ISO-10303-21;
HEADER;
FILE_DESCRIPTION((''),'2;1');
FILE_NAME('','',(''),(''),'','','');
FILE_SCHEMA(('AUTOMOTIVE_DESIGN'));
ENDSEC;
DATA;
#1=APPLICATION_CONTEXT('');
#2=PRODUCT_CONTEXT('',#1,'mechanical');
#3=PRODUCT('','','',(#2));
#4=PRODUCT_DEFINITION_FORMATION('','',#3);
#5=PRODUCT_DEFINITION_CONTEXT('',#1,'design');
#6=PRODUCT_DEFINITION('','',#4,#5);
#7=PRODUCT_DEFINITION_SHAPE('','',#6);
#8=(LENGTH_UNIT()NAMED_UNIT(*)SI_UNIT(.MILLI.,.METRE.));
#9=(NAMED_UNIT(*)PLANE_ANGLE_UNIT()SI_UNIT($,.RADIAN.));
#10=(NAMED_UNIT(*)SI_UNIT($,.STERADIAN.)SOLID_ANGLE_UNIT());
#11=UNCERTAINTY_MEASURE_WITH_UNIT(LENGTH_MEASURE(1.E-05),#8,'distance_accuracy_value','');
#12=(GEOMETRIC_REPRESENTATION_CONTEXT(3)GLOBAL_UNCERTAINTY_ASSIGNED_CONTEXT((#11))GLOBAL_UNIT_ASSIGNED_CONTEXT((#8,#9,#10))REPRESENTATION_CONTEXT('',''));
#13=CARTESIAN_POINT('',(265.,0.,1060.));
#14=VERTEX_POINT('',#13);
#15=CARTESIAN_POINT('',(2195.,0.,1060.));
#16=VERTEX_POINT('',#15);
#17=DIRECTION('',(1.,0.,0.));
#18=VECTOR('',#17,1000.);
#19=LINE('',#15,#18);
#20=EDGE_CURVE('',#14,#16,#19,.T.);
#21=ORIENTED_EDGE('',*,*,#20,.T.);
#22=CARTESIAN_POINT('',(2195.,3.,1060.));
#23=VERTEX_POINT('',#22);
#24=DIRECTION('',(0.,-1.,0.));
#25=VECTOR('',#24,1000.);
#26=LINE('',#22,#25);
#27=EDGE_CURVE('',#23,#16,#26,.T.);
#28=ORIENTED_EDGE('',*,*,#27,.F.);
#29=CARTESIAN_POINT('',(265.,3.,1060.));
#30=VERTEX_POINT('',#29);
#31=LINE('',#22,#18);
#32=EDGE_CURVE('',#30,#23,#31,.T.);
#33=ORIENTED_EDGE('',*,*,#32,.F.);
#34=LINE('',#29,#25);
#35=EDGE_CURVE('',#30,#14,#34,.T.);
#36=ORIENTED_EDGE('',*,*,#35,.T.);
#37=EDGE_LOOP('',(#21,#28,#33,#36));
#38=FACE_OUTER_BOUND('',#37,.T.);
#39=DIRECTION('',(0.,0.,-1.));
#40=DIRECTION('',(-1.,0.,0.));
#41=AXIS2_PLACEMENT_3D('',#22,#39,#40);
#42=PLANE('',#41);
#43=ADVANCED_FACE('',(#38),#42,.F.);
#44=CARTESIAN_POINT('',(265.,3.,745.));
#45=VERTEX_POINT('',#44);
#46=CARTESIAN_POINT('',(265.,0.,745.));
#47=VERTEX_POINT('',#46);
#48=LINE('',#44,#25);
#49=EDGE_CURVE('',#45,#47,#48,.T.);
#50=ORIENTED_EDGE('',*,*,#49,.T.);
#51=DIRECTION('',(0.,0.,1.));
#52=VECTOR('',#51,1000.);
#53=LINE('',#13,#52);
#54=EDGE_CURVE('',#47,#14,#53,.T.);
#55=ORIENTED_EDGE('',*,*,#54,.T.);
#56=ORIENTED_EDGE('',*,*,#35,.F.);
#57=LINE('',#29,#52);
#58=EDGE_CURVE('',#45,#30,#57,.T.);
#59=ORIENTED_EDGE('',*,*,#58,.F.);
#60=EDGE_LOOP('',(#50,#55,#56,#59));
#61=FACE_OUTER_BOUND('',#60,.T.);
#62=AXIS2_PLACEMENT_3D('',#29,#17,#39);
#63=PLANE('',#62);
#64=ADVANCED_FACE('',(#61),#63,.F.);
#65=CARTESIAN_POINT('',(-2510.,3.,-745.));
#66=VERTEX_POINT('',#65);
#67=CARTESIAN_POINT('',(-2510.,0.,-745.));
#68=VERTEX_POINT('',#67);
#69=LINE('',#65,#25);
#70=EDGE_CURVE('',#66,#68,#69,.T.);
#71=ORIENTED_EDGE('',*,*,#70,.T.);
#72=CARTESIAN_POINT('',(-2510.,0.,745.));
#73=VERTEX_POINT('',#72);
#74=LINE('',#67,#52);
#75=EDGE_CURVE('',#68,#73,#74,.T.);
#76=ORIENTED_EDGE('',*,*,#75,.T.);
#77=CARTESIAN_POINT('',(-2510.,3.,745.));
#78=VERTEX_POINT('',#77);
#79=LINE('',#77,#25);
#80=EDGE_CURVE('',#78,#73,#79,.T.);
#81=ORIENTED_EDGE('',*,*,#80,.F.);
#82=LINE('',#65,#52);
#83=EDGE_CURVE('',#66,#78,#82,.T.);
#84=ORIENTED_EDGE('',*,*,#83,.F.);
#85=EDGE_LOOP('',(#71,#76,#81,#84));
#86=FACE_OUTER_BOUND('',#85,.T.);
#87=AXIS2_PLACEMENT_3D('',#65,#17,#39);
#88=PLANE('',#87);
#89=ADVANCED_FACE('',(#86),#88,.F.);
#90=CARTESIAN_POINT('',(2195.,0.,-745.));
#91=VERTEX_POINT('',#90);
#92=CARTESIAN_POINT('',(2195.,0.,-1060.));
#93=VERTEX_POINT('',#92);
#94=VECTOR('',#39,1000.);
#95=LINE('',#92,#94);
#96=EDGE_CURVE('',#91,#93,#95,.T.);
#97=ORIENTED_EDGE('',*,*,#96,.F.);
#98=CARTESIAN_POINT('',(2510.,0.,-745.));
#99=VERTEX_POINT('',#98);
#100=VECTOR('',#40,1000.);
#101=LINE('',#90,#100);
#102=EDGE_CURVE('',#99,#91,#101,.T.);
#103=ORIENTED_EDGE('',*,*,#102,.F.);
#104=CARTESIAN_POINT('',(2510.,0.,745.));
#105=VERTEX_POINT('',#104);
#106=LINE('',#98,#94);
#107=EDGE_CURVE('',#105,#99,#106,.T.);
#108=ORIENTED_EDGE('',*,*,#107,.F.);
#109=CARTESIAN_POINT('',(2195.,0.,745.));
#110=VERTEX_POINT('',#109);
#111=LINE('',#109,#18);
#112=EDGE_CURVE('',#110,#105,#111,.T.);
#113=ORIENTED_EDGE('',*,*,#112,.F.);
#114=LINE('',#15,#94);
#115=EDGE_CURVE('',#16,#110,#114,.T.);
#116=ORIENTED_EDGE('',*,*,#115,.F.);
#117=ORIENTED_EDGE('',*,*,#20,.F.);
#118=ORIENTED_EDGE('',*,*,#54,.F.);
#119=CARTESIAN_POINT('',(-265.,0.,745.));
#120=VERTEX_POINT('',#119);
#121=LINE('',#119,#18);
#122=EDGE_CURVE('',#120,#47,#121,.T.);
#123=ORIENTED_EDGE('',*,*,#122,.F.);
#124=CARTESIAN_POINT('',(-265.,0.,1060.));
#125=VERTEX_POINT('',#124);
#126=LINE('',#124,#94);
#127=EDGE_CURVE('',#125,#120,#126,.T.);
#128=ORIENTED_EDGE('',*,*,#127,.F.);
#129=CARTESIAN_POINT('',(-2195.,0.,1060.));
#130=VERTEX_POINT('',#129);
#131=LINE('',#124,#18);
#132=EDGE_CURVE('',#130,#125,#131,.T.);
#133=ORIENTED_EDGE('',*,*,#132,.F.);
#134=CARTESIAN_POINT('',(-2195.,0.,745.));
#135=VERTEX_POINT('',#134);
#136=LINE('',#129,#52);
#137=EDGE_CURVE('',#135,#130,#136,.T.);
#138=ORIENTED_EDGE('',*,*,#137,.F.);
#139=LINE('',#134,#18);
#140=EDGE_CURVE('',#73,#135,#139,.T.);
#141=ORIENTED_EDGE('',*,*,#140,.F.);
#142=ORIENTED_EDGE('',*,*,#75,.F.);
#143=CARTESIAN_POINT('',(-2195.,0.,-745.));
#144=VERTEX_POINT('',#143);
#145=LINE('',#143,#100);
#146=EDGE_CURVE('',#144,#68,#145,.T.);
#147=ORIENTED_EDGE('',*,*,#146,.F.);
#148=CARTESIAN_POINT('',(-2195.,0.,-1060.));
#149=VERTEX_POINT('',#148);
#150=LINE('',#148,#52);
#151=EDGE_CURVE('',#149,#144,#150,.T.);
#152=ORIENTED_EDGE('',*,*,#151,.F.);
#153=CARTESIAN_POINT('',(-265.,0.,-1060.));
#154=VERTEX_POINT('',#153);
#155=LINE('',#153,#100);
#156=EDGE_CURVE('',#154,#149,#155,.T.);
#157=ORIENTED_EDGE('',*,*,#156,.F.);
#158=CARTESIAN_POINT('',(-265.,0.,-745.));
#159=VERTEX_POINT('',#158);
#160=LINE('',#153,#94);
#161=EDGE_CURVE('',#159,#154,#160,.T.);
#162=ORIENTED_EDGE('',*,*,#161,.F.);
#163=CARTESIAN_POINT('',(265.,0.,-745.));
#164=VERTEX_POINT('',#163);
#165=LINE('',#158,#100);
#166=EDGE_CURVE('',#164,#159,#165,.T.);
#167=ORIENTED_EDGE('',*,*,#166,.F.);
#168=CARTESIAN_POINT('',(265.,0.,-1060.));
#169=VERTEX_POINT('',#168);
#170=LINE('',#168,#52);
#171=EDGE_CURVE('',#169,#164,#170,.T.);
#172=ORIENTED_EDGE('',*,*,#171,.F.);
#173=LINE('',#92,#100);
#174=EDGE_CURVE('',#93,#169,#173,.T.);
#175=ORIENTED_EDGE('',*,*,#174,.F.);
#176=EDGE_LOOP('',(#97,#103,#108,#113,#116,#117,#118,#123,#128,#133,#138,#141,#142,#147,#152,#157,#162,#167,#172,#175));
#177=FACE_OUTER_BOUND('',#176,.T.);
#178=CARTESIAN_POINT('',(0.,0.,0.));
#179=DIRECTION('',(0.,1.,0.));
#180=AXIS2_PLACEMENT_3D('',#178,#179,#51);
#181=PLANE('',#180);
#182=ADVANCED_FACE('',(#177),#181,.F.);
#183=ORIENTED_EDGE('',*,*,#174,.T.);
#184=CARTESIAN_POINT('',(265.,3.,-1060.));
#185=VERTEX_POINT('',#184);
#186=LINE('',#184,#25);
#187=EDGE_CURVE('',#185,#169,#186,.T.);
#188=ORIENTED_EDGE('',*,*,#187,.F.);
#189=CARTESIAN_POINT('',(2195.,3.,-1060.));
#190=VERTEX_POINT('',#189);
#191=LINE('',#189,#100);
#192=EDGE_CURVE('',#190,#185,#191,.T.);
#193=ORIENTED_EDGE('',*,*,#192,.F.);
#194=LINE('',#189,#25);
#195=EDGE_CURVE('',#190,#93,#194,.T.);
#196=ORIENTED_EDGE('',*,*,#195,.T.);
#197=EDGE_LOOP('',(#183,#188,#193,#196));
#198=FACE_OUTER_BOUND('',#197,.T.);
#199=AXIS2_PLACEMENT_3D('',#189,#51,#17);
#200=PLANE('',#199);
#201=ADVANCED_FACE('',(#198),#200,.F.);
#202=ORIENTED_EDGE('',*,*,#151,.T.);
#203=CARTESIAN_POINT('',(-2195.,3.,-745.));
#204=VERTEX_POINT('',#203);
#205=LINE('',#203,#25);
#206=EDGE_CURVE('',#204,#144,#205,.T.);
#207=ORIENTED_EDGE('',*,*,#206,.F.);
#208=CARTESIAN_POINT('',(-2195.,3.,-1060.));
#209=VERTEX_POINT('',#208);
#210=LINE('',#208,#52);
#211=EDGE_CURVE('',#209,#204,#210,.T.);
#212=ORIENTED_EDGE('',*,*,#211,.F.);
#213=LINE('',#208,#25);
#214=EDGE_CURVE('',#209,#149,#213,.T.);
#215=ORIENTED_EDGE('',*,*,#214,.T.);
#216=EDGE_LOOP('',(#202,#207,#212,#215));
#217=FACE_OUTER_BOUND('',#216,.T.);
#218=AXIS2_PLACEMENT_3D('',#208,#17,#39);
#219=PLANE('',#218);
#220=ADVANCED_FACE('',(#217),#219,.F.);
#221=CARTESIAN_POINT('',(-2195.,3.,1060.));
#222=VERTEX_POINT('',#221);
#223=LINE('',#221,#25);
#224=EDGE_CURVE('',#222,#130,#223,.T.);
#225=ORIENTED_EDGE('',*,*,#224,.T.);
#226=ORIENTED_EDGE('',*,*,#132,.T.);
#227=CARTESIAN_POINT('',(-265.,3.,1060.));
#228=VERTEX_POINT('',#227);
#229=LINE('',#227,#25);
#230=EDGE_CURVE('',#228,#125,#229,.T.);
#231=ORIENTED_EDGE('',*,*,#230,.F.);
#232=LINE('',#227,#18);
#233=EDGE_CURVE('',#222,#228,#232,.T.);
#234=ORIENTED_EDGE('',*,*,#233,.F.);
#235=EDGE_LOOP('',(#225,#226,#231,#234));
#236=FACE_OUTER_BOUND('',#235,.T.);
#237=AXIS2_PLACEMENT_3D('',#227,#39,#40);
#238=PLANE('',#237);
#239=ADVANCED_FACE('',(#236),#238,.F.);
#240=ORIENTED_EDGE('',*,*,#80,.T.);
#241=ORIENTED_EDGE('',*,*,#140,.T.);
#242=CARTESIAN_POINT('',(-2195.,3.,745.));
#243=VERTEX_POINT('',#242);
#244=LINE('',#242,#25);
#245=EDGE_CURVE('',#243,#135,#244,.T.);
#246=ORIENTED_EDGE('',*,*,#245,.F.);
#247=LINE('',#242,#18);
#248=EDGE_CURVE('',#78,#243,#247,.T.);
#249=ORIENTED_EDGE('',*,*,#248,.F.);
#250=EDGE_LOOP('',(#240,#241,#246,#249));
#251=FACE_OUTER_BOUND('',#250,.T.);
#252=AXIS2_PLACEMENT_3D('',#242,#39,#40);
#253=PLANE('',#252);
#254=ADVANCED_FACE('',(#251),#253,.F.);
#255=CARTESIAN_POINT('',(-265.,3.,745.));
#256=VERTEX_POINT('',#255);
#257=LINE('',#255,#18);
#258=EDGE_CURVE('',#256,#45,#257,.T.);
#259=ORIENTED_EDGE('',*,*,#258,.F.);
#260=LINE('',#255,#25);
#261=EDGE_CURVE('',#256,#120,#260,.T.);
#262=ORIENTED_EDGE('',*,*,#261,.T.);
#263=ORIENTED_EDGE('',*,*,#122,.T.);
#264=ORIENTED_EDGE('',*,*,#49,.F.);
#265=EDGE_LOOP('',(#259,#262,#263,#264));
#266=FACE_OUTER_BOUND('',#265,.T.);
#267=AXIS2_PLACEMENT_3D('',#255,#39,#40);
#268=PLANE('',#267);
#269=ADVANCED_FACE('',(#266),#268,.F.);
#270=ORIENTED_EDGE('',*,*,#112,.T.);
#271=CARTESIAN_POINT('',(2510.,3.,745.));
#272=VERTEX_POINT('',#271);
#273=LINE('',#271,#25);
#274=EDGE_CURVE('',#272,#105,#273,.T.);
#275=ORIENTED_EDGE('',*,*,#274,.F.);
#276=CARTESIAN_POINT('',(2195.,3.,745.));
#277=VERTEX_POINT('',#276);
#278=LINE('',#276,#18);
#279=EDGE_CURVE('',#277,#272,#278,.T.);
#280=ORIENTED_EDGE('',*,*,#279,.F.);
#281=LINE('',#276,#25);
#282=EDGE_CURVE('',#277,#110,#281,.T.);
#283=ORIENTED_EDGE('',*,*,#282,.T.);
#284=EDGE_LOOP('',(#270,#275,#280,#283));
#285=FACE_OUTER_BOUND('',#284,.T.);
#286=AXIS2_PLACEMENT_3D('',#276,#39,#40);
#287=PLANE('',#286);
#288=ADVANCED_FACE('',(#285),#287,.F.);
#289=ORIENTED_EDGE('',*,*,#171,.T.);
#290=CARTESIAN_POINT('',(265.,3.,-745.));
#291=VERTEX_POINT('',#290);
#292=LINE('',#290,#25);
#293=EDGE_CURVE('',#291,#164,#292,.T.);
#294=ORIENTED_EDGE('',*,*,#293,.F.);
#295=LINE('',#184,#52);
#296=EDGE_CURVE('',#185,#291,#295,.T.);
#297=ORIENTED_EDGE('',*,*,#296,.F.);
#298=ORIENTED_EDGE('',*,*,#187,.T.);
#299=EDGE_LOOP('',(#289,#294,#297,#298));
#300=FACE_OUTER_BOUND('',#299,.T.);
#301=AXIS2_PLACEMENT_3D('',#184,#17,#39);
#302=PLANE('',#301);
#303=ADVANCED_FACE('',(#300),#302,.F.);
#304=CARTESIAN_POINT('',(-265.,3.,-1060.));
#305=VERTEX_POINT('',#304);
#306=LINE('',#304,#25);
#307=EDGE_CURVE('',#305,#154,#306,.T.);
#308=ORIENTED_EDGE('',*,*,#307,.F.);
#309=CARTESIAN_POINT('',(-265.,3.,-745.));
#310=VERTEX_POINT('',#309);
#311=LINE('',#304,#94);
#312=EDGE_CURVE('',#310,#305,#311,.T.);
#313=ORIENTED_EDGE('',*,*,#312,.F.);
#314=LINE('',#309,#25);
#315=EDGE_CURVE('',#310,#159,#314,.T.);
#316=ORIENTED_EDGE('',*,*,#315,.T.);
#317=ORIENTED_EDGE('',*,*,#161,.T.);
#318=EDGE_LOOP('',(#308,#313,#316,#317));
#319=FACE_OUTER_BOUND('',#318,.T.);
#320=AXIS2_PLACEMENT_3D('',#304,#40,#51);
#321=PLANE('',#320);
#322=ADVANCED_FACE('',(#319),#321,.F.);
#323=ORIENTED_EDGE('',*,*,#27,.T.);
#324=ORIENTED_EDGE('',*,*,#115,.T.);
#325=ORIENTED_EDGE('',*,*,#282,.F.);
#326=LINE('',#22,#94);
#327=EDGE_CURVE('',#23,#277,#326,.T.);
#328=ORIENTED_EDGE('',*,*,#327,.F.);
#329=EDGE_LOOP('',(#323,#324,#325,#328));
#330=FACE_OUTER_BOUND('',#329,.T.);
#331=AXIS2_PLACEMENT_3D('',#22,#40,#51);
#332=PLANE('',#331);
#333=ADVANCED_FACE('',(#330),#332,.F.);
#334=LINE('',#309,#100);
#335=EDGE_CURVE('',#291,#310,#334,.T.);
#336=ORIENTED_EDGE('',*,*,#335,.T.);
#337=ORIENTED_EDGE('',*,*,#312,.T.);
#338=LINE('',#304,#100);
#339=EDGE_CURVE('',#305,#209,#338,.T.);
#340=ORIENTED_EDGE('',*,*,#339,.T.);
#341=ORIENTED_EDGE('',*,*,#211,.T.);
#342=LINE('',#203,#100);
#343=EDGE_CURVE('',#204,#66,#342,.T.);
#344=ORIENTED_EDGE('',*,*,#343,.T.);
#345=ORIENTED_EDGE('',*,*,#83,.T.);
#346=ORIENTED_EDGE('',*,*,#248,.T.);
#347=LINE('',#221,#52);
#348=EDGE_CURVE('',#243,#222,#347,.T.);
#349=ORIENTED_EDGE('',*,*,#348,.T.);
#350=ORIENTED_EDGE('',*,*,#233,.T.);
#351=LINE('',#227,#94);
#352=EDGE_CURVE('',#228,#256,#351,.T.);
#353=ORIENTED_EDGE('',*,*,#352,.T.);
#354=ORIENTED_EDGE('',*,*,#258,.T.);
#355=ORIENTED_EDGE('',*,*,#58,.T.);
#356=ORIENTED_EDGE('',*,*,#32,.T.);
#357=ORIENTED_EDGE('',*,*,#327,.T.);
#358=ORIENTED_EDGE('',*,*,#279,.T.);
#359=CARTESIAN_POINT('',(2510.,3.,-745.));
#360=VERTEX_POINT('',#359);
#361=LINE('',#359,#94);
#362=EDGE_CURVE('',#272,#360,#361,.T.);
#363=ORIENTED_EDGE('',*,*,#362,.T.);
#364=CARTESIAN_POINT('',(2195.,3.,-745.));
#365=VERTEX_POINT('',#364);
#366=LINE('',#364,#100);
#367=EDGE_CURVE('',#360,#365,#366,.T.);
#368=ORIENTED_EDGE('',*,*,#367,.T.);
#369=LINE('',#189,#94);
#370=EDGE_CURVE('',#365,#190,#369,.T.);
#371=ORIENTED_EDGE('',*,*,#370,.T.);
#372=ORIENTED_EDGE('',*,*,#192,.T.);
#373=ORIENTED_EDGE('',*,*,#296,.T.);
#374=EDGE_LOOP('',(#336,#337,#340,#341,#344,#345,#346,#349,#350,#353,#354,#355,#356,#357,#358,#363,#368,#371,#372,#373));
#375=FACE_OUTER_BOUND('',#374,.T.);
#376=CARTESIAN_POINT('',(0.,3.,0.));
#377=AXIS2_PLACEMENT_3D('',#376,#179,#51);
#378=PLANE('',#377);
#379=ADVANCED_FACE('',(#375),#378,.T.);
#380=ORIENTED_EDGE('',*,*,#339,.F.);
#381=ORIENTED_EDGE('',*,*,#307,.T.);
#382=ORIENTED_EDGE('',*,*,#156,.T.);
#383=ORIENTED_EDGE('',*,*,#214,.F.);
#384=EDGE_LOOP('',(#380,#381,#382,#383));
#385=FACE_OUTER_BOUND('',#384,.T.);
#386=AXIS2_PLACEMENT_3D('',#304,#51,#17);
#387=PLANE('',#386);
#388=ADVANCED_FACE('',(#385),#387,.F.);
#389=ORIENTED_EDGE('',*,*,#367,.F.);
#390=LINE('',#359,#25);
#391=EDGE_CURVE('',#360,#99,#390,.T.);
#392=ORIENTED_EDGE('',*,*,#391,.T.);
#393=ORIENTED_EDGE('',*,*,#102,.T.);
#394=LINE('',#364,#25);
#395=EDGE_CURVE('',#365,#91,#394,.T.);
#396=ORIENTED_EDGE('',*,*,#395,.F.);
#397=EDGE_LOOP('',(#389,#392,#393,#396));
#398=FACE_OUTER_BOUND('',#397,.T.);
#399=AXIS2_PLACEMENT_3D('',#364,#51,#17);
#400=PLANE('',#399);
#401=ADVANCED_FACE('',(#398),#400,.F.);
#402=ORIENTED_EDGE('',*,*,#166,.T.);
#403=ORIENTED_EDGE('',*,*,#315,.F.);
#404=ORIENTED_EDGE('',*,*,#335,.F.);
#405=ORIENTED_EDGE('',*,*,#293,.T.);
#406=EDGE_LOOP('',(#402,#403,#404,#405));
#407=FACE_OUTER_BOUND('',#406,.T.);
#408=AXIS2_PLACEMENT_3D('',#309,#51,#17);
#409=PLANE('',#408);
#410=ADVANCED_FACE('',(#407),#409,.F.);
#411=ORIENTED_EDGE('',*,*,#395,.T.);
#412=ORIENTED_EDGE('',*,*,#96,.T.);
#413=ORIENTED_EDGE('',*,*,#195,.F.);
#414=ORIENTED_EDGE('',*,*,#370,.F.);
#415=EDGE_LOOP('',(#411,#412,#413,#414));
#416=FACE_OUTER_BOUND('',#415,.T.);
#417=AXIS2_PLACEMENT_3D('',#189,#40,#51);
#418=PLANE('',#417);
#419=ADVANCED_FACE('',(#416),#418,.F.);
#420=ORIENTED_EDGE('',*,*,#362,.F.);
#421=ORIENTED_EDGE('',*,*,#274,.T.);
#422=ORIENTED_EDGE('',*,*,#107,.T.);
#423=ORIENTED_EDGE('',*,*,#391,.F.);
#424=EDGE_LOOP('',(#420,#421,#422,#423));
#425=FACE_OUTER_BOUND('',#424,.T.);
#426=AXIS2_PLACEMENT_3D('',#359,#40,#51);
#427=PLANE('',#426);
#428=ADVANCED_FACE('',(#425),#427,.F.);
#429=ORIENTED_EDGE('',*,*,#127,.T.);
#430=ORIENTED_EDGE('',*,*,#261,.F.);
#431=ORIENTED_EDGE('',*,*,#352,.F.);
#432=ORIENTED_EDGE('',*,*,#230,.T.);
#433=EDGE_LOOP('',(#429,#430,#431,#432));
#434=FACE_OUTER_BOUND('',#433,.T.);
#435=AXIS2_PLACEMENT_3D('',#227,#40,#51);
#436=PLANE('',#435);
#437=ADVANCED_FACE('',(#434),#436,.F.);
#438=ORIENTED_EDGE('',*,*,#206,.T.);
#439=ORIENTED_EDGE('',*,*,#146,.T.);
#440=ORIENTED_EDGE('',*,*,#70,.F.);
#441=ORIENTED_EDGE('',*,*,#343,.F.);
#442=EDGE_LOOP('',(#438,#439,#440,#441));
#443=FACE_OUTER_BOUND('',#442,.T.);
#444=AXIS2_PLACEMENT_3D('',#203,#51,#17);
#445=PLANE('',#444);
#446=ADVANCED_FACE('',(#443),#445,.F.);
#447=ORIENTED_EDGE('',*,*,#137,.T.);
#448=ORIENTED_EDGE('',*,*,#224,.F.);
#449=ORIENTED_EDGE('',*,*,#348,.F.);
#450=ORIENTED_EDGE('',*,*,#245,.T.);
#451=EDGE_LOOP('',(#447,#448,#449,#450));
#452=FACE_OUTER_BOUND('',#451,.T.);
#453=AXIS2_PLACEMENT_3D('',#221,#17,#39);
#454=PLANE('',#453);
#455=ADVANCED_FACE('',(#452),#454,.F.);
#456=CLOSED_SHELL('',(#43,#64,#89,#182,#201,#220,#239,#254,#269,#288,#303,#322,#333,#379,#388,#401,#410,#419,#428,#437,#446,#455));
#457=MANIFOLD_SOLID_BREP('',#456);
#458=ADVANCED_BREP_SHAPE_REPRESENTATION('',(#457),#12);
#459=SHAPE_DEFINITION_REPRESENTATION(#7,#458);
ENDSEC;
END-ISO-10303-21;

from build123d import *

# Parameters (mm, degrees)
BOSS_EXTRUDE_1_DEPTH = 3


with BuildPart() as part:
    # Sketch 1 → Boss-Extrude 1 (new body)
    with BuildSketch(Plane(origin=(0, 0, 0), x_dir=(1, 0, 0), z_dir=(0, 1, 0))):
        Polygon((2195, 1060), (265, 1060), (265, 745), (-265, 745), (-265, 1060), (-2195, 1060), (-2195, 745), (-2510, 745), (-2510, -745), (-2195, -745), (-2195, -1060), (-265, -1060), (-265, -745), (265, -745), (265, -1060), (2195, -1060), (2195, -745), (2510, -745), (2510, 745), (2195, 745), align=None)
    extrude(amount=BOSS_EXTRUDE_1_DEPTH)


solid = part.part
